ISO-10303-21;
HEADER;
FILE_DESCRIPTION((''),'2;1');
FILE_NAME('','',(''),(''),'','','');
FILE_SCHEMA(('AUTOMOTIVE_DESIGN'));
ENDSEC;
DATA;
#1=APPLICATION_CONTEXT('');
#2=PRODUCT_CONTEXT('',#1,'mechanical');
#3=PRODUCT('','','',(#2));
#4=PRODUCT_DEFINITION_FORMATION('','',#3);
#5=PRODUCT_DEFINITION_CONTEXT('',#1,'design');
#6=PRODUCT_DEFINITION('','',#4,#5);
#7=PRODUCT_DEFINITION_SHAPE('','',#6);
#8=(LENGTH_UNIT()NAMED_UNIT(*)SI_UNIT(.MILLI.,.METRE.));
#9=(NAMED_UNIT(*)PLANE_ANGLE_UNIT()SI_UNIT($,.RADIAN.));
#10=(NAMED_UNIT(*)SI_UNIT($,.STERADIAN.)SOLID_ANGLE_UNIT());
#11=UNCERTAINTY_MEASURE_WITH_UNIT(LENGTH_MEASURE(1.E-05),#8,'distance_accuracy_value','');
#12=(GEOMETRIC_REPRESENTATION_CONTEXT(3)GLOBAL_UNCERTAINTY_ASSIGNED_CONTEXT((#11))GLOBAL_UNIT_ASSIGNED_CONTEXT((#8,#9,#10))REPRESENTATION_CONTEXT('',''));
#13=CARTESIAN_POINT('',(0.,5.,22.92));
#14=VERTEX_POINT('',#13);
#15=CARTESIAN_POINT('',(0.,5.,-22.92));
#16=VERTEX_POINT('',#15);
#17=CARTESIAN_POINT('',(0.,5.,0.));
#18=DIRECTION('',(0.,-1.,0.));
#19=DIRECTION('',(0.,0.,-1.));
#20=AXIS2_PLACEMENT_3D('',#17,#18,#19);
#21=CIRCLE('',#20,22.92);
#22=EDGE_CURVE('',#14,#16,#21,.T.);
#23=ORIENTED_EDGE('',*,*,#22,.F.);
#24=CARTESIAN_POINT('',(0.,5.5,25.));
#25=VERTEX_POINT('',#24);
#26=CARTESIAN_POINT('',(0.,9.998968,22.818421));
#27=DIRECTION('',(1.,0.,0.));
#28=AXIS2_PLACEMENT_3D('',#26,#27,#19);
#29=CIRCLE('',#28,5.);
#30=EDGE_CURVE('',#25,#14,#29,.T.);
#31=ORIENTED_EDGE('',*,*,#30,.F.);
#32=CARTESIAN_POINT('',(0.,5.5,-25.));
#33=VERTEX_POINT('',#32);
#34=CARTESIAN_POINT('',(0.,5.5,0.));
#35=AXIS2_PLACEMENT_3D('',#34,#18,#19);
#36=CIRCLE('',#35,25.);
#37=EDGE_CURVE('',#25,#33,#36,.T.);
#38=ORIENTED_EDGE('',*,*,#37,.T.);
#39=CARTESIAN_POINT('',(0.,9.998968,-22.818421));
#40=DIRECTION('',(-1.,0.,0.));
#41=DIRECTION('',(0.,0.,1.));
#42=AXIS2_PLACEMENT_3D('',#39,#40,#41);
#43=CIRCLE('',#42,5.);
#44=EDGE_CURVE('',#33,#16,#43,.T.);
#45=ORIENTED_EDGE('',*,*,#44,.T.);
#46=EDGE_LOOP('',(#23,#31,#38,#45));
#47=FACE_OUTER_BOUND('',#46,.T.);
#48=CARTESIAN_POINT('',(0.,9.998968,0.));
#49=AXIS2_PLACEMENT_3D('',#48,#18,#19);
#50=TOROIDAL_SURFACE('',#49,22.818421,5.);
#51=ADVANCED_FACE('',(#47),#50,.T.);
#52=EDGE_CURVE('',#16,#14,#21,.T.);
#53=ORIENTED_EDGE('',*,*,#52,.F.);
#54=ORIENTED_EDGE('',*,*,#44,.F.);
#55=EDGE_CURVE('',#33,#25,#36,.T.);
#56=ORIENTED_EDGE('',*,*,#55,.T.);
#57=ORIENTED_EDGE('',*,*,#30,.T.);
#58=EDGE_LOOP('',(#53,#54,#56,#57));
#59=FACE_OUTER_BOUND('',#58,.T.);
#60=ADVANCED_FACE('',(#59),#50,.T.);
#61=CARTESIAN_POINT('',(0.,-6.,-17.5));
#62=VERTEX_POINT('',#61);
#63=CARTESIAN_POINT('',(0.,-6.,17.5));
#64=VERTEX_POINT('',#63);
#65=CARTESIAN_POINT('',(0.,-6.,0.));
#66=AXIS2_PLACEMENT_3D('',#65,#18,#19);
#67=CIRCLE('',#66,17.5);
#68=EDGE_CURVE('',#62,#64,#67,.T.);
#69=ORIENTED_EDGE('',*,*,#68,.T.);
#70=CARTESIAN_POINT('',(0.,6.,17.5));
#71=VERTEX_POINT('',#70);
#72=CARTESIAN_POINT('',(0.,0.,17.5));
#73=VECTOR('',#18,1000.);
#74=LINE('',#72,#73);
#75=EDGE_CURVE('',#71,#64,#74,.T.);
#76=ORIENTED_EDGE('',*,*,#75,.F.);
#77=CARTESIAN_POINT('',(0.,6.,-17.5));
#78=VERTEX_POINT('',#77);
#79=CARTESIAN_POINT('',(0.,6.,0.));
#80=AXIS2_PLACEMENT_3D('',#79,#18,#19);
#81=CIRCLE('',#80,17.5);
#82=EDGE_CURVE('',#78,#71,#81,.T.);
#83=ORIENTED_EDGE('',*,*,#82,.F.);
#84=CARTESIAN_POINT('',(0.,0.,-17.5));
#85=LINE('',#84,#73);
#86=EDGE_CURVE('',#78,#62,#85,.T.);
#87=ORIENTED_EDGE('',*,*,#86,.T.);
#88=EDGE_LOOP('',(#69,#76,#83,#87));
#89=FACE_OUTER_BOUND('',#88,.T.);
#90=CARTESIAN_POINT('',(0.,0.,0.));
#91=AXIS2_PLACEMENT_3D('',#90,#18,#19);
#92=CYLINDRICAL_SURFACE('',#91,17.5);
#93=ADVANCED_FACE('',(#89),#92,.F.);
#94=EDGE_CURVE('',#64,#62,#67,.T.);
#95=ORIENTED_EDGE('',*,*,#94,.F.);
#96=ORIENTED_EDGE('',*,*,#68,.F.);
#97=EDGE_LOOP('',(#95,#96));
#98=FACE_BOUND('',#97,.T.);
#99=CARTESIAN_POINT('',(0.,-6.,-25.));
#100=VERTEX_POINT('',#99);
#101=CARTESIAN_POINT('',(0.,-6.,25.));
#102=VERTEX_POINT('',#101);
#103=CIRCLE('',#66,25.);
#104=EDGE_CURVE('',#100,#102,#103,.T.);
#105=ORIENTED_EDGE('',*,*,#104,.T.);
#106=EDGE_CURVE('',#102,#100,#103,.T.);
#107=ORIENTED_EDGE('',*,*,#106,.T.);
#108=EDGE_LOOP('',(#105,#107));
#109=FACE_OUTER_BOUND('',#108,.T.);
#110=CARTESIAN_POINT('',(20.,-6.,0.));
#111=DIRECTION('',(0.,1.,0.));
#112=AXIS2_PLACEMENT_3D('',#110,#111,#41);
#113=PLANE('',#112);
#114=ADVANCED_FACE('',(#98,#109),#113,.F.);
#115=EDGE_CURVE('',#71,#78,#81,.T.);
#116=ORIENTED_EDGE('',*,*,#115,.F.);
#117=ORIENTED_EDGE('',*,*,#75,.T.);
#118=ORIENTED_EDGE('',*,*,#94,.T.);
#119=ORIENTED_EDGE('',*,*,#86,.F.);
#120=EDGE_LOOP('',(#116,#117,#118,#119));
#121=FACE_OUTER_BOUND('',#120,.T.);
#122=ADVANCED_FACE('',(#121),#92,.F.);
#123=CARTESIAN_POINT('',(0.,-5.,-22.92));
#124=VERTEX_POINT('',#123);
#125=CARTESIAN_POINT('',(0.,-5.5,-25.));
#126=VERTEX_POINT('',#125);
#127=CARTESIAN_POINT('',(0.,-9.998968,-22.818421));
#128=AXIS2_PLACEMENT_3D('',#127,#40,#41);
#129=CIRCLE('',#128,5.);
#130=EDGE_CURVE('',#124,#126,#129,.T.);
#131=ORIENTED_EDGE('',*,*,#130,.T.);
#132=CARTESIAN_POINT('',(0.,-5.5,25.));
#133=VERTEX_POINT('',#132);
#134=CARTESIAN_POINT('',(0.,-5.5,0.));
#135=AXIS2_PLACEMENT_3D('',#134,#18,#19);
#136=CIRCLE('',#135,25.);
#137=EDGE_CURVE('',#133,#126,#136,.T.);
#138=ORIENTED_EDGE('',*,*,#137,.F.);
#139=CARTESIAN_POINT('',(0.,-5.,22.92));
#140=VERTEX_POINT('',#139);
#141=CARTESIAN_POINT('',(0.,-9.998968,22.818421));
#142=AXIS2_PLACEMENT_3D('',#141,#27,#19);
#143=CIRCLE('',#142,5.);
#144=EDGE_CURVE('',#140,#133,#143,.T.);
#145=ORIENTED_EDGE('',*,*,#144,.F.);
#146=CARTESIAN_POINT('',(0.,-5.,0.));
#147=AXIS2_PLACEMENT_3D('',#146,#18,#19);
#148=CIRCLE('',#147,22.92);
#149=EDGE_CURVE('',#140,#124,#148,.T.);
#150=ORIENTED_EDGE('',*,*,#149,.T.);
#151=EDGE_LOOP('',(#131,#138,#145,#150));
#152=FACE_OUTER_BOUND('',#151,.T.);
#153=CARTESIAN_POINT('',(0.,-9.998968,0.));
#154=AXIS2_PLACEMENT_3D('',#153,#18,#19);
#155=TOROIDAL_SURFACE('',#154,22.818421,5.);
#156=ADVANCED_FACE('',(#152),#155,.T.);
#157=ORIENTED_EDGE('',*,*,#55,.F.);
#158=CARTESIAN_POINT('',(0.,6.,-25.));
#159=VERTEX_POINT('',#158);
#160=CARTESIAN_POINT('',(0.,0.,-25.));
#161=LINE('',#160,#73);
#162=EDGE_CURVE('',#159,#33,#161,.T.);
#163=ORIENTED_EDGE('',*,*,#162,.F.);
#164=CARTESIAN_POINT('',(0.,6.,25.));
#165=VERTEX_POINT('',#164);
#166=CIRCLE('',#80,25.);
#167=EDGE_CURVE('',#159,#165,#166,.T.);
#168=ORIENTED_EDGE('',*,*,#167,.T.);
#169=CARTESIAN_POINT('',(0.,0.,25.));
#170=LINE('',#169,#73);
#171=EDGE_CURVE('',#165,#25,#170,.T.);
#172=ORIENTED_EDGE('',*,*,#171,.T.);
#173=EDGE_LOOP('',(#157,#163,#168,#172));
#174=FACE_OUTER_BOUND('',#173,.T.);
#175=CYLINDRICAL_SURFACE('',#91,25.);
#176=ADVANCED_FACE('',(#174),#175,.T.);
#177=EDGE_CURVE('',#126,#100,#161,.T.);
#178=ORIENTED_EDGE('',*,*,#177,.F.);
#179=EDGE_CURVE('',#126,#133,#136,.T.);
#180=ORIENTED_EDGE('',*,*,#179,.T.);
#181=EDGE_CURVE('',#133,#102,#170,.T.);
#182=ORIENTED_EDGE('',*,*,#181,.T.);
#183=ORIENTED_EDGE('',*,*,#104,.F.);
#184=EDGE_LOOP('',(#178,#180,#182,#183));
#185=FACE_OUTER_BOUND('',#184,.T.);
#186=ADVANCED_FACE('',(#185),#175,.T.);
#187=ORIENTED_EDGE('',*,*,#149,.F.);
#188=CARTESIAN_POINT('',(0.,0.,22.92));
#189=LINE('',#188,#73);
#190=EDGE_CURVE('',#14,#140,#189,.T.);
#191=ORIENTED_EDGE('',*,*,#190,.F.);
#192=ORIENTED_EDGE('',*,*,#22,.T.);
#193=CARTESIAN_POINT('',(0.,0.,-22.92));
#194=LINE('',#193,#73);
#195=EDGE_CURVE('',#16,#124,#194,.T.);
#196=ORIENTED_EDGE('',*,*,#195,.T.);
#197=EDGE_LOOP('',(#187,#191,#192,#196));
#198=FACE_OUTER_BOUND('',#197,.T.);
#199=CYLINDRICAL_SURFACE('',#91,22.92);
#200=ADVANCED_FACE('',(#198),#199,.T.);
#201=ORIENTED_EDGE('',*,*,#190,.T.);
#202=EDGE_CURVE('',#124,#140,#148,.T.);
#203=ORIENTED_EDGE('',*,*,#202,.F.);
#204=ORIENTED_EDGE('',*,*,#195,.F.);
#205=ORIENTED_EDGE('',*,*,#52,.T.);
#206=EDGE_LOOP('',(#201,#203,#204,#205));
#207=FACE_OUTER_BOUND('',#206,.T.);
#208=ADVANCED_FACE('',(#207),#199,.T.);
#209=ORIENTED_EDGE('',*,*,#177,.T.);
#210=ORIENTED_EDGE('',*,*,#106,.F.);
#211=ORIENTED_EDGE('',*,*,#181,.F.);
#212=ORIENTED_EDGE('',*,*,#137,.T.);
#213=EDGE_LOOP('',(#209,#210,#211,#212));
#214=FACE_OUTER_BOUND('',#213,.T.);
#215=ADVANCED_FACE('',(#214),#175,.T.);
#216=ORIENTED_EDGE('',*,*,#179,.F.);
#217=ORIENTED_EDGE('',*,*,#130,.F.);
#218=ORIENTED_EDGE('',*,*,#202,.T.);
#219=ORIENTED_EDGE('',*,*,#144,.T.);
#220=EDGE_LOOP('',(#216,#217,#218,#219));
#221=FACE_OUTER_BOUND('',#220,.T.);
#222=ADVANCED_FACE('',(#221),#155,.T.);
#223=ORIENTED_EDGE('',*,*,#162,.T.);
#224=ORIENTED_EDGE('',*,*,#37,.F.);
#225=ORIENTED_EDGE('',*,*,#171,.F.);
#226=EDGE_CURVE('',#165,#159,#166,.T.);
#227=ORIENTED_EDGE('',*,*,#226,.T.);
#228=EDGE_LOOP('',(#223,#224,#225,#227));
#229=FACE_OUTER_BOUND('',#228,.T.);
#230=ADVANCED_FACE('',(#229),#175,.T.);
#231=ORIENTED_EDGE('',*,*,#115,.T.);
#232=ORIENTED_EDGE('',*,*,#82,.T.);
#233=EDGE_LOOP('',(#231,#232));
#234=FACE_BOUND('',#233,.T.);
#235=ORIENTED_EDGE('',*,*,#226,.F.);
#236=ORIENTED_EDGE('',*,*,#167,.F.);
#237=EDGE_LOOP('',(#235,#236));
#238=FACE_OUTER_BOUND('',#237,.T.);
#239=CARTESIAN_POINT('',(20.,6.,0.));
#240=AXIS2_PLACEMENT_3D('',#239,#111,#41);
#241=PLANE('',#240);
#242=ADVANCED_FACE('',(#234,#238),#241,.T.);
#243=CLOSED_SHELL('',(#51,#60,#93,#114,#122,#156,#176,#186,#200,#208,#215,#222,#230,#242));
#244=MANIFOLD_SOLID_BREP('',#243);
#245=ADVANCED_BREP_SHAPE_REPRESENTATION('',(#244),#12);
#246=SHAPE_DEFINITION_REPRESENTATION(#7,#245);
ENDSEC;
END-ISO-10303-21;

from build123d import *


with BuildPart() as part:
    # Sketch1 → Revolve1 (revolve)
    with BuildSketch(Plane.XY, mode=Mode.PRIVATE) as revolve1_sk:
        Polygon((22.92, -5), (22.92, 5), (20, 5), (20, 6), (17.5, 6), (17.5, -6), (20, -6), (20, -5), align=None)
    revolve(revolve1_sk.sketch.rotate(Axis((0, 0, 0), (0, 1, 0)), 90), axis=Axis((0, 0, 0), (0, 1, 0)))

    # Sketch2 → Revolve2 (revolve)
    with BuildSketch(Plane.XY, mode=Mode.PRIVATE) as revolve2_sk:
        with BuildLine():
            Line((20, 5), (22.92, 5))
            ThreePointArc((22.92, 5), (23.9870538, 5.137456193), (25, 5.5))
            Line((25, 5.5), (25, 6))
            Line((25, 6), (20, 6))
            Line((20, 6), (20, 5))
        make_face()
        with BuildLine():
            Line((25, -5.5), (25, -6))
            Line((25, -6), (20, -6))
            Line((20, -6), (20, -5))
            Line((20, -5), (22.92, -5))
            ThreePointArc((22.92, -5), (23.9870538, -5.137456193), (25, -5.5))
        make_face()
    revolve(revolve2_sk.sketch.rotate(Axis((0, 0, 0), (0, 1, 0)), 90), axis=Axis((0, 0, 0), (0, 1, 0)))


solid = part.part
